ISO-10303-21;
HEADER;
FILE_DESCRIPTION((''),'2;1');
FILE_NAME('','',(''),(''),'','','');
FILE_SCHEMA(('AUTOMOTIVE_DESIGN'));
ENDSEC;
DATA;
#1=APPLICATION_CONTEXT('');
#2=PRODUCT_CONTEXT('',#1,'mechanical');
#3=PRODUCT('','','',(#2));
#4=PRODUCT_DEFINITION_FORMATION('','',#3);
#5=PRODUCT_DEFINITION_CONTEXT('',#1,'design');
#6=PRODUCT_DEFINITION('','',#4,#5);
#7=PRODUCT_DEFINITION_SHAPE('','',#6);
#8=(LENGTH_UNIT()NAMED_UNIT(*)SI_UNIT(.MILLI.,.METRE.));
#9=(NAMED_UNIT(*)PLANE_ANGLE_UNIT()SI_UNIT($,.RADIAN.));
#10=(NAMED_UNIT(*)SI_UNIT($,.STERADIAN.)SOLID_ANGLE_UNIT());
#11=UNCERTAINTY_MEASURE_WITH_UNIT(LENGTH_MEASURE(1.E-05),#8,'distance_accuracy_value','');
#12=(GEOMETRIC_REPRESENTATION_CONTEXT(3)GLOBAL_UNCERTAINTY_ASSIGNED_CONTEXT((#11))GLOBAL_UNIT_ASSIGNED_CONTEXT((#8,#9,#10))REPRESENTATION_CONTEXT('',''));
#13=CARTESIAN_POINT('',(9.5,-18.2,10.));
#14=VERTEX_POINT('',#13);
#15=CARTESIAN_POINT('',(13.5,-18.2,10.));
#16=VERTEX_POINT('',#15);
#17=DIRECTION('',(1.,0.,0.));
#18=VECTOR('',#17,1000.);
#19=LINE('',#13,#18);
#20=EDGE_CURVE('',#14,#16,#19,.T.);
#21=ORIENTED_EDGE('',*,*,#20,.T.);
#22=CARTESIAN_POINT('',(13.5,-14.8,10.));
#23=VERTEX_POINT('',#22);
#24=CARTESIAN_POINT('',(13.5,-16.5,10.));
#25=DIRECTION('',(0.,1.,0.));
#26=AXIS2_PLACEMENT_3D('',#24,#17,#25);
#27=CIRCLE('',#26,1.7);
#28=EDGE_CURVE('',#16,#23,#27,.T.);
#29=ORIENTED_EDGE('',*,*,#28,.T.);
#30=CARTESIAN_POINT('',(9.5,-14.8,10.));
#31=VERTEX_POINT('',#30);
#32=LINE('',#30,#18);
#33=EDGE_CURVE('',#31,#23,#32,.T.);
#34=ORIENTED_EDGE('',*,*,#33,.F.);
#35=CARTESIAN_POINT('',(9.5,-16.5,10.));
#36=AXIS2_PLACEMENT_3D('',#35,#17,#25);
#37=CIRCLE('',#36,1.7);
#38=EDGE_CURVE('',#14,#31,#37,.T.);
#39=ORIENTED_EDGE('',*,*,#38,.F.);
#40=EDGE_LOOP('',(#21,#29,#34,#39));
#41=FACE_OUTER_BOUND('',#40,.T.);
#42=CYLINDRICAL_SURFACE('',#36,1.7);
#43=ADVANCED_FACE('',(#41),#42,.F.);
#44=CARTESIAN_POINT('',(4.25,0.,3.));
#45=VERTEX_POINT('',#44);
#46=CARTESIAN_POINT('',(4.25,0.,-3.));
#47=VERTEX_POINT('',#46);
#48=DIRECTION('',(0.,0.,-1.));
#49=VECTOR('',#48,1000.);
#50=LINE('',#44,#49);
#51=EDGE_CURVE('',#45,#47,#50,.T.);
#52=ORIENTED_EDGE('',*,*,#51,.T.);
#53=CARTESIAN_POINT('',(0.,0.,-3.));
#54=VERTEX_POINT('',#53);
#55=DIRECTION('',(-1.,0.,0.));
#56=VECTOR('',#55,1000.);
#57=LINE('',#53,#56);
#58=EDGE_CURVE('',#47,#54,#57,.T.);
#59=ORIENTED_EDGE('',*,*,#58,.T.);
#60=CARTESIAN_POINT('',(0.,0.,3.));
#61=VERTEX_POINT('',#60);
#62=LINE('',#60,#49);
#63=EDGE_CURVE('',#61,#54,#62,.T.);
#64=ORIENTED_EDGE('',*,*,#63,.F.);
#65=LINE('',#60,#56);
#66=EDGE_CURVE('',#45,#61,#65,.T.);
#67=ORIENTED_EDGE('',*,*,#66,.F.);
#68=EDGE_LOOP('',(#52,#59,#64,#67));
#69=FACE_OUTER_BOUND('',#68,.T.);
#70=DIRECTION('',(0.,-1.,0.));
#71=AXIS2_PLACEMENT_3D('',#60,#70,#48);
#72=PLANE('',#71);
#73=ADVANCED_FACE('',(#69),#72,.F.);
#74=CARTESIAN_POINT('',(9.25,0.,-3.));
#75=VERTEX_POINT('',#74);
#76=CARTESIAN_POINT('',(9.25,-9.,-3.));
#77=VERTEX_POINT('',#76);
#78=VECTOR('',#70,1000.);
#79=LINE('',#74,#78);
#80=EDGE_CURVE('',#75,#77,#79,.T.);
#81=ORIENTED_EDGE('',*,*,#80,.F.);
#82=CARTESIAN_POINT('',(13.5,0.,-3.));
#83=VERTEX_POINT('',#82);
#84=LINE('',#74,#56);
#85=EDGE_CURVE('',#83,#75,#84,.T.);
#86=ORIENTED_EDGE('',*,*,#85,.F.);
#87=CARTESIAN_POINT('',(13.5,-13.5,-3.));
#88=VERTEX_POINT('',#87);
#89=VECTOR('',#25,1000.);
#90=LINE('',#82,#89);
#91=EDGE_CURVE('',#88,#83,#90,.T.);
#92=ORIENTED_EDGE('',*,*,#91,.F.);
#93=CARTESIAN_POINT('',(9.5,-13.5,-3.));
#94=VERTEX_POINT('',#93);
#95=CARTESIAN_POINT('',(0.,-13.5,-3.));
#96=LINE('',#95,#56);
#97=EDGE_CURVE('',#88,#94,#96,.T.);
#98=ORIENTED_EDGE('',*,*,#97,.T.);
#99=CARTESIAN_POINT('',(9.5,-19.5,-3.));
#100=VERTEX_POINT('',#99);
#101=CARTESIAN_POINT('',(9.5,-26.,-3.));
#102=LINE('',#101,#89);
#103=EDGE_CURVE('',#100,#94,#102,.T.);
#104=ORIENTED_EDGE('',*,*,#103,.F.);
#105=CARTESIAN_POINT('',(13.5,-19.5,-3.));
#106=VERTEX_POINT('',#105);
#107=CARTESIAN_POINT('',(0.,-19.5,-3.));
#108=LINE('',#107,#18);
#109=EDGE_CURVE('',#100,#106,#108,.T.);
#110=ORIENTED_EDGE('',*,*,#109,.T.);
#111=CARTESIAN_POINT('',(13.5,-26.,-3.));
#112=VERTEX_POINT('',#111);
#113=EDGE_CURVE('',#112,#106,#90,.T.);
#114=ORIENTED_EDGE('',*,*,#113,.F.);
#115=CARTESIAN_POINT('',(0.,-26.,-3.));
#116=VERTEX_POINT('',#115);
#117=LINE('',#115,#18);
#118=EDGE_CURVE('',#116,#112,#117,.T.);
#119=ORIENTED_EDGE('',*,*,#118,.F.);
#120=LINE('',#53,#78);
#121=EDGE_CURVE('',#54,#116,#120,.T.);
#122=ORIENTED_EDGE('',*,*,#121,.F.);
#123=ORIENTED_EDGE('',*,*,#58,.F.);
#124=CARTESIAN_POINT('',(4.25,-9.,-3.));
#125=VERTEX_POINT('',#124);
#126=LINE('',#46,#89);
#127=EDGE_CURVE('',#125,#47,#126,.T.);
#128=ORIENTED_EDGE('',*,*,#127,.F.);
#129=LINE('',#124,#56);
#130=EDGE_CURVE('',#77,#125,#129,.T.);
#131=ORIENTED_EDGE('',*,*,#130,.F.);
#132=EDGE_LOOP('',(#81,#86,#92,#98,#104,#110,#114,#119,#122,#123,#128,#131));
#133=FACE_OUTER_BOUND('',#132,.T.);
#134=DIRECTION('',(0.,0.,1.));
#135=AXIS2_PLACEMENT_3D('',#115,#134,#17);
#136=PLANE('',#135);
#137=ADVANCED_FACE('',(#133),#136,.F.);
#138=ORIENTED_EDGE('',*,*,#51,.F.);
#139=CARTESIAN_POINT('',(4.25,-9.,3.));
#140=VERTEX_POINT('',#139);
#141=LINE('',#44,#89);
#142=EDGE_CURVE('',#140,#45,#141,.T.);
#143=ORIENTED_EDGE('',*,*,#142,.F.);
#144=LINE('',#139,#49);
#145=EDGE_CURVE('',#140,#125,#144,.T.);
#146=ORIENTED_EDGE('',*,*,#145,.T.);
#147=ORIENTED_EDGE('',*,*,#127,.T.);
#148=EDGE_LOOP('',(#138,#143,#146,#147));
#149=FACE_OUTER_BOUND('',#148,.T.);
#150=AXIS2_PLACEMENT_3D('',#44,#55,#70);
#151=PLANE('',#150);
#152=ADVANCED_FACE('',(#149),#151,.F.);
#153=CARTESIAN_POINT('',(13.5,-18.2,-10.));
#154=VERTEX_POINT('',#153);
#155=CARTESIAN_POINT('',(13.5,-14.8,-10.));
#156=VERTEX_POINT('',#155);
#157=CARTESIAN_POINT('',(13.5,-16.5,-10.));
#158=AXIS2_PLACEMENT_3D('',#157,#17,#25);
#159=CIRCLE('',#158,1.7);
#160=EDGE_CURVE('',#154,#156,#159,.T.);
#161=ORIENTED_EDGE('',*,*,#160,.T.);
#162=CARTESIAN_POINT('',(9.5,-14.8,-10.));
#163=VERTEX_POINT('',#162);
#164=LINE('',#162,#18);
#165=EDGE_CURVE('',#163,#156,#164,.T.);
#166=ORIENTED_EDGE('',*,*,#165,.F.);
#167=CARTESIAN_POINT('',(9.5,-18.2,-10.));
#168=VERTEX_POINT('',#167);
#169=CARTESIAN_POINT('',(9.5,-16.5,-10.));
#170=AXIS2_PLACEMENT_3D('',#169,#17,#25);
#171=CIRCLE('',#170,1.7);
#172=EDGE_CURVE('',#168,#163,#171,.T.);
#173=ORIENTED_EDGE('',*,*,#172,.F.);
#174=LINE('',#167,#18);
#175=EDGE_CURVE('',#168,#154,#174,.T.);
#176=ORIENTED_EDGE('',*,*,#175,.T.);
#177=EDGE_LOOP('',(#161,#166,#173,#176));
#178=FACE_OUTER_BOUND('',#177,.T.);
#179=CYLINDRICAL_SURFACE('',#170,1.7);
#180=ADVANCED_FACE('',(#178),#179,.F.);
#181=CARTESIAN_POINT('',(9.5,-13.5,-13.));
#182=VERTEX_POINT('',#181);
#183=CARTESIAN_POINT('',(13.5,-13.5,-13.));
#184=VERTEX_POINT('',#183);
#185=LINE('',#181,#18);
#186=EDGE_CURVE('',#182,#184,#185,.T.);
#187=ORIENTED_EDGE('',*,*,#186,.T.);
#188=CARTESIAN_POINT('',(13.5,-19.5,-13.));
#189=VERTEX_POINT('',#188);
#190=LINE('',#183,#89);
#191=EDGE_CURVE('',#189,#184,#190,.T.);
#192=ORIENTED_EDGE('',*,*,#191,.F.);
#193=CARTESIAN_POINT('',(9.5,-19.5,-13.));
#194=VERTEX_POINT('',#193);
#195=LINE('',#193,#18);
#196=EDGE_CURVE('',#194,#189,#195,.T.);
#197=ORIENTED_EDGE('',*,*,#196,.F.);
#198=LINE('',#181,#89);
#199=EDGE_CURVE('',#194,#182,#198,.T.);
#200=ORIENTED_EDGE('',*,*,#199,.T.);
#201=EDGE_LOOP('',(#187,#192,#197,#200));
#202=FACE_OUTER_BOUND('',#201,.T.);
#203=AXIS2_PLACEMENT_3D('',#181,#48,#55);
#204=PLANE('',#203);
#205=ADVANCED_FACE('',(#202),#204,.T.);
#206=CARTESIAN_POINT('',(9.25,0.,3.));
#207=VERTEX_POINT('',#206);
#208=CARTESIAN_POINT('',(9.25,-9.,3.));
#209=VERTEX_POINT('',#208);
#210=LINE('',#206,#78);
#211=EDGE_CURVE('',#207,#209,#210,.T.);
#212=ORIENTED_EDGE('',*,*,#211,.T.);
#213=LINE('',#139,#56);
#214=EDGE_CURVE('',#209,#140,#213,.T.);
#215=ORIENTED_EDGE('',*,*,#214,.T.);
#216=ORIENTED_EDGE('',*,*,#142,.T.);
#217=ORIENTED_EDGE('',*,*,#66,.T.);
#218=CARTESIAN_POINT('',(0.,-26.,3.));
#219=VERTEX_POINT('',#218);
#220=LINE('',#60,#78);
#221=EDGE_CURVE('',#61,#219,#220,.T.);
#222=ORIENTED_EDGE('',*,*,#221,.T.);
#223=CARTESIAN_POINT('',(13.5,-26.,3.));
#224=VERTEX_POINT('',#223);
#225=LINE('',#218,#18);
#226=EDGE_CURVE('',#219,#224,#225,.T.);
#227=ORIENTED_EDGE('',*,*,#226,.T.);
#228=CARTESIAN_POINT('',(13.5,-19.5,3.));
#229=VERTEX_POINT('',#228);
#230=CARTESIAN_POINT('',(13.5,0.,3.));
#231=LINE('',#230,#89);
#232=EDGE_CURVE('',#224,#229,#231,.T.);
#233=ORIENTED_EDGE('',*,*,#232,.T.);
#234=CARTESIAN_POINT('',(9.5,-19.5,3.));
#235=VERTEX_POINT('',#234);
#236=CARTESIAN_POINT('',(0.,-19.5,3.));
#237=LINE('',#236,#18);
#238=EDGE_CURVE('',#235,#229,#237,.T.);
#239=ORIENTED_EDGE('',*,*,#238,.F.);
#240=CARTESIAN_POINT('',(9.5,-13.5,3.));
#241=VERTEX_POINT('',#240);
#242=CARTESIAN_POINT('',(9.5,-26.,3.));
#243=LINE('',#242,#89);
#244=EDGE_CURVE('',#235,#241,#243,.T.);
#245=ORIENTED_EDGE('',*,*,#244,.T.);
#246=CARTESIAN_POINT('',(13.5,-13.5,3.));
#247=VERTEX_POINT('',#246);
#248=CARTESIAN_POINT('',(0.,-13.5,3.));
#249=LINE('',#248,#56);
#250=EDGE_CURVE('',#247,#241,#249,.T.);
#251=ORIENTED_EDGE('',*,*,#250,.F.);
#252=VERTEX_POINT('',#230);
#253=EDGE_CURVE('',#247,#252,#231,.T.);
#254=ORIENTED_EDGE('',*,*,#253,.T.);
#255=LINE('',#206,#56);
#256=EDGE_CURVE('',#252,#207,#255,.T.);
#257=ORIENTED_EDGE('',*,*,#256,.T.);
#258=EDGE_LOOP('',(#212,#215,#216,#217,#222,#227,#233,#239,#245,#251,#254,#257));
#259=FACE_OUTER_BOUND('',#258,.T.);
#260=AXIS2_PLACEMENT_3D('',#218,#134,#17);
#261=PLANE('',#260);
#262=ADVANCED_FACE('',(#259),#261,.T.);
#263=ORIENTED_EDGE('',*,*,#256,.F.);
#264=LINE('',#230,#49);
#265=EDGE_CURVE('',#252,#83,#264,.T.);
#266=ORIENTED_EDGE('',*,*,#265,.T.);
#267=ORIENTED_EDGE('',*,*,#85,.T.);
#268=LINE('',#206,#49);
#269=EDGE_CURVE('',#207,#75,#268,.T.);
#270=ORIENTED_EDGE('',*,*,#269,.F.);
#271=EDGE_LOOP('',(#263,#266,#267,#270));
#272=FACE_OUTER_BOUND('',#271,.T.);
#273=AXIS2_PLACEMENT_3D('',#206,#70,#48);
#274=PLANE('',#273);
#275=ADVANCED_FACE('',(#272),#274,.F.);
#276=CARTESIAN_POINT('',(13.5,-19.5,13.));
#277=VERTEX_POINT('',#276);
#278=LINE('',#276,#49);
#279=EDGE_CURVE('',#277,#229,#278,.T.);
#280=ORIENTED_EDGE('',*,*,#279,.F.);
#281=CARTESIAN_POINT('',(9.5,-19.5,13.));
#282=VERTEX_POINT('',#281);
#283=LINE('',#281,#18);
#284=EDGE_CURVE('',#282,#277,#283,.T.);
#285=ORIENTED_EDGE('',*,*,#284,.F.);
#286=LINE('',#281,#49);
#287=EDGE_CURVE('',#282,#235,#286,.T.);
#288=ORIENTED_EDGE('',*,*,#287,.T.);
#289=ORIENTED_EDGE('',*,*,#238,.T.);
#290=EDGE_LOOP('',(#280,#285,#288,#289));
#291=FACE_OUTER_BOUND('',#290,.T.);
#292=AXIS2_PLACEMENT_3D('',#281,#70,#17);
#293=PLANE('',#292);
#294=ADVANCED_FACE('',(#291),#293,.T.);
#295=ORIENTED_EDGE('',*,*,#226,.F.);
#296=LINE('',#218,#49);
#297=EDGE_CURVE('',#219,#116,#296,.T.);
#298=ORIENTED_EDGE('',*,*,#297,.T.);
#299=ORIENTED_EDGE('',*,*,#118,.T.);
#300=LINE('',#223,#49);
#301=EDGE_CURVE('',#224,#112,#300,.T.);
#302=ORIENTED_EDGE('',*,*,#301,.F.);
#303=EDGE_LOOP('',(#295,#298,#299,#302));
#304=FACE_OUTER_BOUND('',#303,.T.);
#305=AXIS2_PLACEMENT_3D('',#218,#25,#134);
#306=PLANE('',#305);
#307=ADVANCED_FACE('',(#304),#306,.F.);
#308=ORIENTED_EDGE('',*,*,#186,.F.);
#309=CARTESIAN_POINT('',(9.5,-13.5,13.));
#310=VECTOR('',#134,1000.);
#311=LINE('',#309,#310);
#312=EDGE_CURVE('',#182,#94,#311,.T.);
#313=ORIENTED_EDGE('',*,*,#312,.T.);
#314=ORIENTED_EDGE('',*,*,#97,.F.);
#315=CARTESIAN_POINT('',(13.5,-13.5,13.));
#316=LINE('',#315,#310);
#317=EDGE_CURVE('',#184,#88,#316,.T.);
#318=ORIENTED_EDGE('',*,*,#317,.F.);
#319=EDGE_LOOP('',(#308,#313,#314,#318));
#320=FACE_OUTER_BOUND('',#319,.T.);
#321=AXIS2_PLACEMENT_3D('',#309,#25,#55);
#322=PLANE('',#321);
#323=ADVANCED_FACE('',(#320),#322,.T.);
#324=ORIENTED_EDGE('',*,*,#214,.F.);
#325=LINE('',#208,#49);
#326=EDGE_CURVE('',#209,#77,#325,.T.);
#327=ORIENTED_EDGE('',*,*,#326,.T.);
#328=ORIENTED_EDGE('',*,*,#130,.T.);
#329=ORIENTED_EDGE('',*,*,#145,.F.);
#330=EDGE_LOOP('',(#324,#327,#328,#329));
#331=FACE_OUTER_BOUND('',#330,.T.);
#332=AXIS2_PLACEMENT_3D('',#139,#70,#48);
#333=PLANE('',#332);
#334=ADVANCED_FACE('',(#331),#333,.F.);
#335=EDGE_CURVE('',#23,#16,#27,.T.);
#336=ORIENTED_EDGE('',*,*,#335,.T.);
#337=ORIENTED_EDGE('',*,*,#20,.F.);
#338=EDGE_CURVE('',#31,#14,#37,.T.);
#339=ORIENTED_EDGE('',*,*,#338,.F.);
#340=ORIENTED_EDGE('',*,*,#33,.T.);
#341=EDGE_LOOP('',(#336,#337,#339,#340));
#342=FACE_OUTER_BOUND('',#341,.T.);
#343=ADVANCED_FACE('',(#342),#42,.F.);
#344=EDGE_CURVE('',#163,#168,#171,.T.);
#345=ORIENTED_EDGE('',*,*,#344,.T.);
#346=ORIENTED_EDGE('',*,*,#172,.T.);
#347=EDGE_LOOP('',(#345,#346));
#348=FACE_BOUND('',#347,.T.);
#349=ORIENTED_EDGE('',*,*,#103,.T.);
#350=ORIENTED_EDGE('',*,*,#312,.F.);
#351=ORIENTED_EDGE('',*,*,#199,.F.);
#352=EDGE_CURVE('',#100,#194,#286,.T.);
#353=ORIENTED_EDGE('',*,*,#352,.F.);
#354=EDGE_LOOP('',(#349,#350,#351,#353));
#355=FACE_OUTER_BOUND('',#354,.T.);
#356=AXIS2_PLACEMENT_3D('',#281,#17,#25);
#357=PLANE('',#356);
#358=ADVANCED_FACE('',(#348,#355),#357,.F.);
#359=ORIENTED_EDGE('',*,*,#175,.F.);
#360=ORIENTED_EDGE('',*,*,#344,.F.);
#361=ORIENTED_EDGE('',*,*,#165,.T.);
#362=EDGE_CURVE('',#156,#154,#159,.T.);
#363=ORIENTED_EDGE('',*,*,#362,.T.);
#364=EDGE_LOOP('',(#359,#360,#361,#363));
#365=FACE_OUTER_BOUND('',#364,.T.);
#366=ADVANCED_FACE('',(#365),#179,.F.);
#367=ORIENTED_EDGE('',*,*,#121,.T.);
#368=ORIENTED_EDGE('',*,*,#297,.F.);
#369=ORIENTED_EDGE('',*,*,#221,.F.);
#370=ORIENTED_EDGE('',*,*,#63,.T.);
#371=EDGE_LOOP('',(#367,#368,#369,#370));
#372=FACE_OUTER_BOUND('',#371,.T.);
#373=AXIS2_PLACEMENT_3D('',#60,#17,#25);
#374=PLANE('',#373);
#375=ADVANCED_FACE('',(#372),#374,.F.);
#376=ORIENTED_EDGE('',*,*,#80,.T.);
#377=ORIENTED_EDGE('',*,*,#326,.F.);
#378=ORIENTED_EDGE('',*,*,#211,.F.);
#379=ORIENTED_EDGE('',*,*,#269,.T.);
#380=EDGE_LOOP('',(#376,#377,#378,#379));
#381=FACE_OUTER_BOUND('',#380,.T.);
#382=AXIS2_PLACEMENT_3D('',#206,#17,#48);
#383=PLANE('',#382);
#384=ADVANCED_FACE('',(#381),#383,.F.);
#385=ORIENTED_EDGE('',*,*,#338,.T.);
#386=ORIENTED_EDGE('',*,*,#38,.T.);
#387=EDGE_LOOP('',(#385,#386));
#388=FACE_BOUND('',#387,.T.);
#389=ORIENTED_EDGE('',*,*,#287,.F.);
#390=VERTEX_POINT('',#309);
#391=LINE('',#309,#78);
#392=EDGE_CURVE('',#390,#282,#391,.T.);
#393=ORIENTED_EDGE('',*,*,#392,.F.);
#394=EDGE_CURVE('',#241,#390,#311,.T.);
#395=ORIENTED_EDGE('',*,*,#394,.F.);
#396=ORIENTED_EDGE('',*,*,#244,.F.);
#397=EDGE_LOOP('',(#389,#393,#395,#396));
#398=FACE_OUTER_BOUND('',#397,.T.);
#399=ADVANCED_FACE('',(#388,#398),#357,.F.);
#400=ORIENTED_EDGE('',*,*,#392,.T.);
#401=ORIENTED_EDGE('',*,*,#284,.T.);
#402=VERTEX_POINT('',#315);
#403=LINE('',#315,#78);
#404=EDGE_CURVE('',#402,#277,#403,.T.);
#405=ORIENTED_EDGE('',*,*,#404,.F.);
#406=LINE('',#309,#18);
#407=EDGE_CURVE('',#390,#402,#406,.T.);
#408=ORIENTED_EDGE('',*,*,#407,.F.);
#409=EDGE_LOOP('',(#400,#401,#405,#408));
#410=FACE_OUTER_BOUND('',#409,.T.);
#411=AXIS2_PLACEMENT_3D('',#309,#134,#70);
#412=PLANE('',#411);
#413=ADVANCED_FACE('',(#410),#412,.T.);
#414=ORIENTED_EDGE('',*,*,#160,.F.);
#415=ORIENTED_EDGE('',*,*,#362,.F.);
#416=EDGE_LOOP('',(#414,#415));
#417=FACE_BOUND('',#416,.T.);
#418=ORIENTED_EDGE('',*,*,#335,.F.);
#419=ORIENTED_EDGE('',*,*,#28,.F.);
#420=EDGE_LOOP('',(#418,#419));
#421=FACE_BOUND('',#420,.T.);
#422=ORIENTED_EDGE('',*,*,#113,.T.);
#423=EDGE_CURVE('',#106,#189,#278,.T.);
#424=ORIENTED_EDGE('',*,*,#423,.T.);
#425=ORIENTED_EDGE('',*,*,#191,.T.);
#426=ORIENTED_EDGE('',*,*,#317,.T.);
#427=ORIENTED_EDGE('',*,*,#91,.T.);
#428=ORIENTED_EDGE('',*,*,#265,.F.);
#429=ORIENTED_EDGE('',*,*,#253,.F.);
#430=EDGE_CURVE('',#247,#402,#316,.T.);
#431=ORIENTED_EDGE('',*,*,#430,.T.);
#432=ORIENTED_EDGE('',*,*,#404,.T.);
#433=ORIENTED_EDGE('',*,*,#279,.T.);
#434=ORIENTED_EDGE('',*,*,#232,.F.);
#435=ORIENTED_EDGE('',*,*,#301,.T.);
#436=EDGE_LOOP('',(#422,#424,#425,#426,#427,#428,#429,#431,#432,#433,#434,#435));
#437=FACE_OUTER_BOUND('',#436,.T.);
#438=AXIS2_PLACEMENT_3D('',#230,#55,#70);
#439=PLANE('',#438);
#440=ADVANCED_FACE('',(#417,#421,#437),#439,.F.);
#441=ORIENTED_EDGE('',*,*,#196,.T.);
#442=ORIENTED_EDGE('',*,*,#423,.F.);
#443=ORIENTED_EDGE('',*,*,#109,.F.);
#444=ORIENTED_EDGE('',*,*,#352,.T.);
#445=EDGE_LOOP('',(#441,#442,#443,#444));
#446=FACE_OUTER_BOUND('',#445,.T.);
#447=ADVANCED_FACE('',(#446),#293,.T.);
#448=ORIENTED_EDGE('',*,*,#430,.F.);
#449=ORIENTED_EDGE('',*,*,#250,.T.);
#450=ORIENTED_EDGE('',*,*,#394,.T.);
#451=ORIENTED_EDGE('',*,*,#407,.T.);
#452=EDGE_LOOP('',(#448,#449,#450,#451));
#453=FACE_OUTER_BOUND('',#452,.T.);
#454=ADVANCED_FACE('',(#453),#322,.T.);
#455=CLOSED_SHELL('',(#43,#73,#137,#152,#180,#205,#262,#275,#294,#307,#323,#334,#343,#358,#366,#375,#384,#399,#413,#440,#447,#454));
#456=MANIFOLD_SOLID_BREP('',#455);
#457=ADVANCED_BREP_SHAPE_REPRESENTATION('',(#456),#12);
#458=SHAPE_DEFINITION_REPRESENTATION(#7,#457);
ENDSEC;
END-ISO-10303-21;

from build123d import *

# Parameters (mm, degrees)
BOSS_EXTRUDE1_DEPTH = 3
SKETCH2_W           = 26
SKETCH2_H           = 6
SKETCH2_R           = 1.7
BOSS_EXTRUDE2_DEPTH = 4


with BuildPart() as part:
    # Sketch1 → Boss-Extrude1 (new, symmetric)
    with BuildSketch(Plane.XY):
        Polygon((9.25, 0), (13.5, 0), (13.5, -26), (0, -26), (0, 0), (4.25, 0), (4.25, -9), (9.25, -9), align=None)
    extrude(amount=BOSS_EXTRUDE1_DEPTH, both=True)

    # Sketch2 → Boss-Extrude2 (add)
    with BuildSketch(Plane(origin=(13.5, 0, 0), x_dir=(0, 0, -1), z_dir=(1, 0, 0))):
        with Locations((0, -16.5)):
            Rectangle(SKETCH2_W, SKETCH2_H)
        with Locations(Location((-10, -16.5, 0), (0, 0, 90))):
            Circle(SKETCH2_R, mode=Mode.SUBTRACT)
        with Locations(Location((10, -16.5, 0), (0, 0, 90))):
            Circle(SKETCH2_R, mode=Mode.SUBTRACT)
    extrude(amount=-BOSS_EXTRUDE2_DEPTH)


solid = part.part
